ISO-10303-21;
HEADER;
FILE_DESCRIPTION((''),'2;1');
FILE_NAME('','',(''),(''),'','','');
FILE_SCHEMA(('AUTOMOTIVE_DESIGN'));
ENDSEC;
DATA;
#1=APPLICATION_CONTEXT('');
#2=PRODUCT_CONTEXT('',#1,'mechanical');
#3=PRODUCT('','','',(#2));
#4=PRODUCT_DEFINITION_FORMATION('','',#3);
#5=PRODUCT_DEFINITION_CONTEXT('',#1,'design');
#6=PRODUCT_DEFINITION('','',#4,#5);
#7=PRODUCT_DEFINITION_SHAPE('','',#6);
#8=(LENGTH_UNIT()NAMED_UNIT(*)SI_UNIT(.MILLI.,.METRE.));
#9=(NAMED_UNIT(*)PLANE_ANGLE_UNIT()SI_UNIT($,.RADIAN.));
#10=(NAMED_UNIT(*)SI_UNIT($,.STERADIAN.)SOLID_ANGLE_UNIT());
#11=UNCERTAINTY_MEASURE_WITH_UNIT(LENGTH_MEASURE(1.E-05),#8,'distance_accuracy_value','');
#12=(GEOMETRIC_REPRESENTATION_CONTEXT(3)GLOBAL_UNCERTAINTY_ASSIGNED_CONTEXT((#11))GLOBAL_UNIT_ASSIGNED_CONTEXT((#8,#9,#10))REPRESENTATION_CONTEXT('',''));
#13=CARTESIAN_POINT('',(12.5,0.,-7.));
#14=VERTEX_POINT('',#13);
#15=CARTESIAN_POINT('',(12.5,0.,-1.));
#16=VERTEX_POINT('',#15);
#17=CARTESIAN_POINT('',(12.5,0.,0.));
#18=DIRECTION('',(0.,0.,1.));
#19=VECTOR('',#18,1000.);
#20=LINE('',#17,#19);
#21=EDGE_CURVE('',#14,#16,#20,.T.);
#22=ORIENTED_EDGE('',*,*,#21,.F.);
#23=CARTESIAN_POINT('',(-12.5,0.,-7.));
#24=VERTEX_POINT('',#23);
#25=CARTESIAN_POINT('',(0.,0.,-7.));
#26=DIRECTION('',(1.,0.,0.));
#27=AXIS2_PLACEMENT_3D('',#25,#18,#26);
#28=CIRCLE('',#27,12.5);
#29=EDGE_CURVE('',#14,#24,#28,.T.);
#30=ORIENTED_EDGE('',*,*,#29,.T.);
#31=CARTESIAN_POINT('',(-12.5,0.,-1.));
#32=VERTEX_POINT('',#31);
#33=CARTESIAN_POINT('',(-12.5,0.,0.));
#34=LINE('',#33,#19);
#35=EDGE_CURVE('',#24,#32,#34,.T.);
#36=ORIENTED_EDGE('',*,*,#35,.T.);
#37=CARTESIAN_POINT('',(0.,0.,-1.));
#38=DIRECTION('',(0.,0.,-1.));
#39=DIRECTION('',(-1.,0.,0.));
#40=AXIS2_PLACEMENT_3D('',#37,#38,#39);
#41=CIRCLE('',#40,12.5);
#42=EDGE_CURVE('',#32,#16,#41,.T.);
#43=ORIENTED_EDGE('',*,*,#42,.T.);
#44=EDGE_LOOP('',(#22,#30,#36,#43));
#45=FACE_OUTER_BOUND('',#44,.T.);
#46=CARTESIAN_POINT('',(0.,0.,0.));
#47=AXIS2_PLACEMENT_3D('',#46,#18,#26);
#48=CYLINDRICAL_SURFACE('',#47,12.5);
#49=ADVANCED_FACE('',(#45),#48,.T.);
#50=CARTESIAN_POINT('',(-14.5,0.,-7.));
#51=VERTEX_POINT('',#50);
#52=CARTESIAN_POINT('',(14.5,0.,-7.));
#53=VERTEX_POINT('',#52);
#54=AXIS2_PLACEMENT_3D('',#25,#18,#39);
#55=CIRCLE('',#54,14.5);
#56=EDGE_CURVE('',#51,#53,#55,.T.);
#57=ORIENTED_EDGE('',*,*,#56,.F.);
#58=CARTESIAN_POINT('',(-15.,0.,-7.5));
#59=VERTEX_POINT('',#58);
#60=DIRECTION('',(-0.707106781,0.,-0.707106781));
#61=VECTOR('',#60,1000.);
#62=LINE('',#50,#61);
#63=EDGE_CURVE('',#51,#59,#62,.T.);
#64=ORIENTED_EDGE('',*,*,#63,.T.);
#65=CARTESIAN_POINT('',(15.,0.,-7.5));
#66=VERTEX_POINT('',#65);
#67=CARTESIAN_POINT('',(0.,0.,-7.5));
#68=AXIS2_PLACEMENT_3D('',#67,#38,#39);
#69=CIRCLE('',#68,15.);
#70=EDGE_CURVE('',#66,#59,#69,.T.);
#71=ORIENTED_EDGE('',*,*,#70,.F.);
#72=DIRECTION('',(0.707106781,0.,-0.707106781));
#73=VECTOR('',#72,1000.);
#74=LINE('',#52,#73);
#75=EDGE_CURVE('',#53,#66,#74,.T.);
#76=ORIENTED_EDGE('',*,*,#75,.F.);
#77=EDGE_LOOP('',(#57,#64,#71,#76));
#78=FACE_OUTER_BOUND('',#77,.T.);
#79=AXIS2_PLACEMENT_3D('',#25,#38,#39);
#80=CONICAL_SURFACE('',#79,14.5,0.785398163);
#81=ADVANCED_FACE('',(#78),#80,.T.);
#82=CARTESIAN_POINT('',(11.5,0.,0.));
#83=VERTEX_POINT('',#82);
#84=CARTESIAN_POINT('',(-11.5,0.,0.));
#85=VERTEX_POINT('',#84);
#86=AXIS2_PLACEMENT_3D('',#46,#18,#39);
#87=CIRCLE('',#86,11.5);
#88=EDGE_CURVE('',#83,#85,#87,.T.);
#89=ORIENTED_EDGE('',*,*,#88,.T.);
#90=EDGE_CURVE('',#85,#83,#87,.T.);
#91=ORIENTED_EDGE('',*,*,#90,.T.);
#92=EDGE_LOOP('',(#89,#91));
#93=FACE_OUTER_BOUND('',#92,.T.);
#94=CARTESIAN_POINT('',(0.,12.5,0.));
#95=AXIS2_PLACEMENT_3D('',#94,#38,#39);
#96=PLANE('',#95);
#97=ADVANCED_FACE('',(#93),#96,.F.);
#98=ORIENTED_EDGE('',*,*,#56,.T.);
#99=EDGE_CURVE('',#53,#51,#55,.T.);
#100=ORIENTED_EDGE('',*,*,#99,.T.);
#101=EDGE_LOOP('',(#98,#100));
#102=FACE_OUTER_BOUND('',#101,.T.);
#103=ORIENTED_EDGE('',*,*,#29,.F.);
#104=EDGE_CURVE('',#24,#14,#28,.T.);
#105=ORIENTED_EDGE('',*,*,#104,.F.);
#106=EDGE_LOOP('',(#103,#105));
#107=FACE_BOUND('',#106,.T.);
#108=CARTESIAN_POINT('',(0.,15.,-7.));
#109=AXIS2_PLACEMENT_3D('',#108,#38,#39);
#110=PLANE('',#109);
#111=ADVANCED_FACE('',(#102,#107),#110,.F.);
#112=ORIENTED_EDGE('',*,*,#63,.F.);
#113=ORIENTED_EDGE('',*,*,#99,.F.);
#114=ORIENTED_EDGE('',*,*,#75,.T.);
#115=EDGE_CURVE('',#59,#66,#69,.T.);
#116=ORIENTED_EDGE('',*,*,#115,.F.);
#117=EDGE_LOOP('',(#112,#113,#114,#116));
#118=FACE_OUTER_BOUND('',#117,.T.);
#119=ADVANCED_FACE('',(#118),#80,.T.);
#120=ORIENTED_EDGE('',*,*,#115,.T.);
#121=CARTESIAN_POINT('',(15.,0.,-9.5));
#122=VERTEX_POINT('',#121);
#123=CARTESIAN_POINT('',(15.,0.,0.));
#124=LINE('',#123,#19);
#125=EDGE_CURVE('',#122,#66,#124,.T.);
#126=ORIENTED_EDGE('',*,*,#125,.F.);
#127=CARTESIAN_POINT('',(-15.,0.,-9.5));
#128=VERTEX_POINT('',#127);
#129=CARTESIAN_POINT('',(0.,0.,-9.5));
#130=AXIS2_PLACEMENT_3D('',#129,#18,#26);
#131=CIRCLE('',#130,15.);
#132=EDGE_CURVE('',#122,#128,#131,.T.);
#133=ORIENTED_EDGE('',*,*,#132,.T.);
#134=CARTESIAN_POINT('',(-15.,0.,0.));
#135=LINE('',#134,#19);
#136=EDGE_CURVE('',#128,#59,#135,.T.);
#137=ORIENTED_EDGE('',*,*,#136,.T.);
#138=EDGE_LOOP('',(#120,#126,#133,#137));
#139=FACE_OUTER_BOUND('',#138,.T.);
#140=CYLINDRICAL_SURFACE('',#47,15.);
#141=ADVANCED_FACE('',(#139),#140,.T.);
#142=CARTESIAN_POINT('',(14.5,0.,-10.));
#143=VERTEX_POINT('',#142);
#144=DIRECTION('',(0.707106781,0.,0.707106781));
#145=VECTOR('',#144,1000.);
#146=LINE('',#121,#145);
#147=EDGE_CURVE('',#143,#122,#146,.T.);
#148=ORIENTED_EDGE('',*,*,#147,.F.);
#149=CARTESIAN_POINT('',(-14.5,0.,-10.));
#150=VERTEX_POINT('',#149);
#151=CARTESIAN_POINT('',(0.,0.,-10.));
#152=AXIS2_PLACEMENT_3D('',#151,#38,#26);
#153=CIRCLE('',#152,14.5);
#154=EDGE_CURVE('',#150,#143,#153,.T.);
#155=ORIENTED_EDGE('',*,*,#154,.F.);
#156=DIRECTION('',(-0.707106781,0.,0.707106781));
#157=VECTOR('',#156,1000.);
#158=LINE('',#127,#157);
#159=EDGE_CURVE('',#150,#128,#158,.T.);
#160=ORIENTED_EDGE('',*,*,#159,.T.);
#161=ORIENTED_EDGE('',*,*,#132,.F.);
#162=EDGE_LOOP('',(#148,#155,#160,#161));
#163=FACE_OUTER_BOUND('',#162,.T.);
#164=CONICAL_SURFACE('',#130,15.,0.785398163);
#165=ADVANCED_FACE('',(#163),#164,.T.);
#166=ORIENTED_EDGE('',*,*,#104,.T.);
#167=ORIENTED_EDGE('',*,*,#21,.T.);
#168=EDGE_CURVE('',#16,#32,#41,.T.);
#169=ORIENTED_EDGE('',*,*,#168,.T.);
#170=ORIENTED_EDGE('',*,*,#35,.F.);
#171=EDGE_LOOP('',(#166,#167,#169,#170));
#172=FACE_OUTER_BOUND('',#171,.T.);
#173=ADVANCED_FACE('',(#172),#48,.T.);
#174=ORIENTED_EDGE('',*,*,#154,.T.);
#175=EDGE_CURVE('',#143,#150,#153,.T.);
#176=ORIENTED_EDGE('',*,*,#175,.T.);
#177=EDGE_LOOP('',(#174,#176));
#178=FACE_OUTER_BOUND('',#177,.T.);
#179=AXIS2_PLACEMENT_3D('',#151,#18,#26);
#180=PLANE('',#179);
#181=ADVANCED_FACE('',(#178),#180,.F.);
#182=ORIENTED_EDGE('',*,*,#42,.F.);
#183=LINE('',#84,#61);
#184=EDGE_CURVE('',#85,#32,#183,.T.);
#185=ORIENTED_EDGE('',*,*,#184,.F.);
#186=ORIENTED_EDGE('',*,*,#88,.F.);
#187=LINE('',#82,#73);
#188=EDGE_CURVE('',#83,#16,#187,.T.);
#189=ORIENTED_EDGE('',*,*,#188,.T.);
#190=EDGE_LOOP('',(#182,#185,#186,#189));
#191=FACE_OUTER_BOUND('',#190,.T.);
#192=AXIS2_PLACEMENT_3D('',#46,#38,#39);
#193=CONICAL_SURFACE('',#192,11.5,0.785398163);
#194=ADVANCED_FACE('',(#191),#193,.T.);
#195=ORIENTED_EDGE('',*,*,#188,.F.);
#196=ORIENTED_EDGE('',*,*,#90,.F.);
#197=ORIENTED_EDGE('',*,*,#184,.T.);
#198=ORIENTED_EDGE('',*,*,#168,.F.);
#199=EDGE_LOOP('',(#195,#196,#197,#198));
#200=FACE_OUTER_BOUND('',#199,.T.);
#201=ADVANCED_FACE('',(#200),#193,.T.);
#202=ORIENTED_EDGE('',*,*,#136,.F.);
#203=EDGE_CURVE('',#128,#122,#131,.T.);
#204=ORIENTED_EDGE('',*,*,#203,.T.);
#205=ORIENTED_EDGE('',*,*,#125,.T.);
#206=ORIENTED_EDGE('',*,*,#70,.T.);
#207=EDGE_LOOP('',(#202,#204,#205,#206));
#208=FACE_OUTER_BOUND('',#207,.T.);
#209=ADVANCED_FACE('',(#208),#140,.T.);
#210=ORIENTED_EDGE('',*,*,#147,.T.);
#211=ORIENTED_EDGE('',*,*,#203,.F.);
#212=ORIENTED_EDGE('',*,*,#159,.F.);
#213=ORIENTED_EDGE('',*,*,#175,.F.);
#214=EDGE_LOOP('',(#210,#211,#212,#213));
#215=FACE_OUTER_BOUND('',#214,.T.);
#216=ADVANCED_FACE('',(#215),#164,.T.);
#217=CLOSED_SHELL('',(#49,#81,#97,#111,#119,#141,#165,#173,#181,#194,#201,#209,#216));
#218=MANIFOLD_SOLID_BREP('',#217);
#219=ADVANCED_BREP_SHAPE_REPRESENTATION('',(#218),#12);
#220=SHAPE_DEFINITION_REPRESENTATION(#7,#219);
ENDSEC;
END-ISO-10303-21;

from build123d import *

# Parameters (mm, degrees)
CHAMFER1_SIZE = 1
CHAMFER2_SIZE = 0.5


with BuildPart() as part:
    # Sketch1 → Revolve1 (revolve)
    with BuildSketch(Plane(origin=(0, 0, 0), x_dir=(0, 0, -1), z_dir=(1, 0, 0)), mode=Mode.PRIVATE) as revolve1_sk:
        Polygon((10, 0), (10, 15), (7, 15), (7, 12.5), (0, 12.5), (0, 0), align=None)
    revolve(revolve1_sk.sketch.rotate(Axis((0, 0, 0), (0, 0, -1)), 90), axis=Axis((0, 0, 0), (0, 0, -1)))

    # Chamfer1
    chamfer1_edges = [part.edges().sort_by_distance(p)[0] for p in [
        (-12.5, 0, 0),
    ]]
    chamfer(chamfer1_edges, length=CHAMFER1_SIZE)

    # Chamfer2
    chamfer2_edges = [part.edges().sort_by_distance(p)[0] for p in [
        (-15, 0, -7),
        (-15, 0, -10),
    ]]
    chamfer(chamfer2_edges, length=CHAMFER2_SIZE)


solid = part.part
